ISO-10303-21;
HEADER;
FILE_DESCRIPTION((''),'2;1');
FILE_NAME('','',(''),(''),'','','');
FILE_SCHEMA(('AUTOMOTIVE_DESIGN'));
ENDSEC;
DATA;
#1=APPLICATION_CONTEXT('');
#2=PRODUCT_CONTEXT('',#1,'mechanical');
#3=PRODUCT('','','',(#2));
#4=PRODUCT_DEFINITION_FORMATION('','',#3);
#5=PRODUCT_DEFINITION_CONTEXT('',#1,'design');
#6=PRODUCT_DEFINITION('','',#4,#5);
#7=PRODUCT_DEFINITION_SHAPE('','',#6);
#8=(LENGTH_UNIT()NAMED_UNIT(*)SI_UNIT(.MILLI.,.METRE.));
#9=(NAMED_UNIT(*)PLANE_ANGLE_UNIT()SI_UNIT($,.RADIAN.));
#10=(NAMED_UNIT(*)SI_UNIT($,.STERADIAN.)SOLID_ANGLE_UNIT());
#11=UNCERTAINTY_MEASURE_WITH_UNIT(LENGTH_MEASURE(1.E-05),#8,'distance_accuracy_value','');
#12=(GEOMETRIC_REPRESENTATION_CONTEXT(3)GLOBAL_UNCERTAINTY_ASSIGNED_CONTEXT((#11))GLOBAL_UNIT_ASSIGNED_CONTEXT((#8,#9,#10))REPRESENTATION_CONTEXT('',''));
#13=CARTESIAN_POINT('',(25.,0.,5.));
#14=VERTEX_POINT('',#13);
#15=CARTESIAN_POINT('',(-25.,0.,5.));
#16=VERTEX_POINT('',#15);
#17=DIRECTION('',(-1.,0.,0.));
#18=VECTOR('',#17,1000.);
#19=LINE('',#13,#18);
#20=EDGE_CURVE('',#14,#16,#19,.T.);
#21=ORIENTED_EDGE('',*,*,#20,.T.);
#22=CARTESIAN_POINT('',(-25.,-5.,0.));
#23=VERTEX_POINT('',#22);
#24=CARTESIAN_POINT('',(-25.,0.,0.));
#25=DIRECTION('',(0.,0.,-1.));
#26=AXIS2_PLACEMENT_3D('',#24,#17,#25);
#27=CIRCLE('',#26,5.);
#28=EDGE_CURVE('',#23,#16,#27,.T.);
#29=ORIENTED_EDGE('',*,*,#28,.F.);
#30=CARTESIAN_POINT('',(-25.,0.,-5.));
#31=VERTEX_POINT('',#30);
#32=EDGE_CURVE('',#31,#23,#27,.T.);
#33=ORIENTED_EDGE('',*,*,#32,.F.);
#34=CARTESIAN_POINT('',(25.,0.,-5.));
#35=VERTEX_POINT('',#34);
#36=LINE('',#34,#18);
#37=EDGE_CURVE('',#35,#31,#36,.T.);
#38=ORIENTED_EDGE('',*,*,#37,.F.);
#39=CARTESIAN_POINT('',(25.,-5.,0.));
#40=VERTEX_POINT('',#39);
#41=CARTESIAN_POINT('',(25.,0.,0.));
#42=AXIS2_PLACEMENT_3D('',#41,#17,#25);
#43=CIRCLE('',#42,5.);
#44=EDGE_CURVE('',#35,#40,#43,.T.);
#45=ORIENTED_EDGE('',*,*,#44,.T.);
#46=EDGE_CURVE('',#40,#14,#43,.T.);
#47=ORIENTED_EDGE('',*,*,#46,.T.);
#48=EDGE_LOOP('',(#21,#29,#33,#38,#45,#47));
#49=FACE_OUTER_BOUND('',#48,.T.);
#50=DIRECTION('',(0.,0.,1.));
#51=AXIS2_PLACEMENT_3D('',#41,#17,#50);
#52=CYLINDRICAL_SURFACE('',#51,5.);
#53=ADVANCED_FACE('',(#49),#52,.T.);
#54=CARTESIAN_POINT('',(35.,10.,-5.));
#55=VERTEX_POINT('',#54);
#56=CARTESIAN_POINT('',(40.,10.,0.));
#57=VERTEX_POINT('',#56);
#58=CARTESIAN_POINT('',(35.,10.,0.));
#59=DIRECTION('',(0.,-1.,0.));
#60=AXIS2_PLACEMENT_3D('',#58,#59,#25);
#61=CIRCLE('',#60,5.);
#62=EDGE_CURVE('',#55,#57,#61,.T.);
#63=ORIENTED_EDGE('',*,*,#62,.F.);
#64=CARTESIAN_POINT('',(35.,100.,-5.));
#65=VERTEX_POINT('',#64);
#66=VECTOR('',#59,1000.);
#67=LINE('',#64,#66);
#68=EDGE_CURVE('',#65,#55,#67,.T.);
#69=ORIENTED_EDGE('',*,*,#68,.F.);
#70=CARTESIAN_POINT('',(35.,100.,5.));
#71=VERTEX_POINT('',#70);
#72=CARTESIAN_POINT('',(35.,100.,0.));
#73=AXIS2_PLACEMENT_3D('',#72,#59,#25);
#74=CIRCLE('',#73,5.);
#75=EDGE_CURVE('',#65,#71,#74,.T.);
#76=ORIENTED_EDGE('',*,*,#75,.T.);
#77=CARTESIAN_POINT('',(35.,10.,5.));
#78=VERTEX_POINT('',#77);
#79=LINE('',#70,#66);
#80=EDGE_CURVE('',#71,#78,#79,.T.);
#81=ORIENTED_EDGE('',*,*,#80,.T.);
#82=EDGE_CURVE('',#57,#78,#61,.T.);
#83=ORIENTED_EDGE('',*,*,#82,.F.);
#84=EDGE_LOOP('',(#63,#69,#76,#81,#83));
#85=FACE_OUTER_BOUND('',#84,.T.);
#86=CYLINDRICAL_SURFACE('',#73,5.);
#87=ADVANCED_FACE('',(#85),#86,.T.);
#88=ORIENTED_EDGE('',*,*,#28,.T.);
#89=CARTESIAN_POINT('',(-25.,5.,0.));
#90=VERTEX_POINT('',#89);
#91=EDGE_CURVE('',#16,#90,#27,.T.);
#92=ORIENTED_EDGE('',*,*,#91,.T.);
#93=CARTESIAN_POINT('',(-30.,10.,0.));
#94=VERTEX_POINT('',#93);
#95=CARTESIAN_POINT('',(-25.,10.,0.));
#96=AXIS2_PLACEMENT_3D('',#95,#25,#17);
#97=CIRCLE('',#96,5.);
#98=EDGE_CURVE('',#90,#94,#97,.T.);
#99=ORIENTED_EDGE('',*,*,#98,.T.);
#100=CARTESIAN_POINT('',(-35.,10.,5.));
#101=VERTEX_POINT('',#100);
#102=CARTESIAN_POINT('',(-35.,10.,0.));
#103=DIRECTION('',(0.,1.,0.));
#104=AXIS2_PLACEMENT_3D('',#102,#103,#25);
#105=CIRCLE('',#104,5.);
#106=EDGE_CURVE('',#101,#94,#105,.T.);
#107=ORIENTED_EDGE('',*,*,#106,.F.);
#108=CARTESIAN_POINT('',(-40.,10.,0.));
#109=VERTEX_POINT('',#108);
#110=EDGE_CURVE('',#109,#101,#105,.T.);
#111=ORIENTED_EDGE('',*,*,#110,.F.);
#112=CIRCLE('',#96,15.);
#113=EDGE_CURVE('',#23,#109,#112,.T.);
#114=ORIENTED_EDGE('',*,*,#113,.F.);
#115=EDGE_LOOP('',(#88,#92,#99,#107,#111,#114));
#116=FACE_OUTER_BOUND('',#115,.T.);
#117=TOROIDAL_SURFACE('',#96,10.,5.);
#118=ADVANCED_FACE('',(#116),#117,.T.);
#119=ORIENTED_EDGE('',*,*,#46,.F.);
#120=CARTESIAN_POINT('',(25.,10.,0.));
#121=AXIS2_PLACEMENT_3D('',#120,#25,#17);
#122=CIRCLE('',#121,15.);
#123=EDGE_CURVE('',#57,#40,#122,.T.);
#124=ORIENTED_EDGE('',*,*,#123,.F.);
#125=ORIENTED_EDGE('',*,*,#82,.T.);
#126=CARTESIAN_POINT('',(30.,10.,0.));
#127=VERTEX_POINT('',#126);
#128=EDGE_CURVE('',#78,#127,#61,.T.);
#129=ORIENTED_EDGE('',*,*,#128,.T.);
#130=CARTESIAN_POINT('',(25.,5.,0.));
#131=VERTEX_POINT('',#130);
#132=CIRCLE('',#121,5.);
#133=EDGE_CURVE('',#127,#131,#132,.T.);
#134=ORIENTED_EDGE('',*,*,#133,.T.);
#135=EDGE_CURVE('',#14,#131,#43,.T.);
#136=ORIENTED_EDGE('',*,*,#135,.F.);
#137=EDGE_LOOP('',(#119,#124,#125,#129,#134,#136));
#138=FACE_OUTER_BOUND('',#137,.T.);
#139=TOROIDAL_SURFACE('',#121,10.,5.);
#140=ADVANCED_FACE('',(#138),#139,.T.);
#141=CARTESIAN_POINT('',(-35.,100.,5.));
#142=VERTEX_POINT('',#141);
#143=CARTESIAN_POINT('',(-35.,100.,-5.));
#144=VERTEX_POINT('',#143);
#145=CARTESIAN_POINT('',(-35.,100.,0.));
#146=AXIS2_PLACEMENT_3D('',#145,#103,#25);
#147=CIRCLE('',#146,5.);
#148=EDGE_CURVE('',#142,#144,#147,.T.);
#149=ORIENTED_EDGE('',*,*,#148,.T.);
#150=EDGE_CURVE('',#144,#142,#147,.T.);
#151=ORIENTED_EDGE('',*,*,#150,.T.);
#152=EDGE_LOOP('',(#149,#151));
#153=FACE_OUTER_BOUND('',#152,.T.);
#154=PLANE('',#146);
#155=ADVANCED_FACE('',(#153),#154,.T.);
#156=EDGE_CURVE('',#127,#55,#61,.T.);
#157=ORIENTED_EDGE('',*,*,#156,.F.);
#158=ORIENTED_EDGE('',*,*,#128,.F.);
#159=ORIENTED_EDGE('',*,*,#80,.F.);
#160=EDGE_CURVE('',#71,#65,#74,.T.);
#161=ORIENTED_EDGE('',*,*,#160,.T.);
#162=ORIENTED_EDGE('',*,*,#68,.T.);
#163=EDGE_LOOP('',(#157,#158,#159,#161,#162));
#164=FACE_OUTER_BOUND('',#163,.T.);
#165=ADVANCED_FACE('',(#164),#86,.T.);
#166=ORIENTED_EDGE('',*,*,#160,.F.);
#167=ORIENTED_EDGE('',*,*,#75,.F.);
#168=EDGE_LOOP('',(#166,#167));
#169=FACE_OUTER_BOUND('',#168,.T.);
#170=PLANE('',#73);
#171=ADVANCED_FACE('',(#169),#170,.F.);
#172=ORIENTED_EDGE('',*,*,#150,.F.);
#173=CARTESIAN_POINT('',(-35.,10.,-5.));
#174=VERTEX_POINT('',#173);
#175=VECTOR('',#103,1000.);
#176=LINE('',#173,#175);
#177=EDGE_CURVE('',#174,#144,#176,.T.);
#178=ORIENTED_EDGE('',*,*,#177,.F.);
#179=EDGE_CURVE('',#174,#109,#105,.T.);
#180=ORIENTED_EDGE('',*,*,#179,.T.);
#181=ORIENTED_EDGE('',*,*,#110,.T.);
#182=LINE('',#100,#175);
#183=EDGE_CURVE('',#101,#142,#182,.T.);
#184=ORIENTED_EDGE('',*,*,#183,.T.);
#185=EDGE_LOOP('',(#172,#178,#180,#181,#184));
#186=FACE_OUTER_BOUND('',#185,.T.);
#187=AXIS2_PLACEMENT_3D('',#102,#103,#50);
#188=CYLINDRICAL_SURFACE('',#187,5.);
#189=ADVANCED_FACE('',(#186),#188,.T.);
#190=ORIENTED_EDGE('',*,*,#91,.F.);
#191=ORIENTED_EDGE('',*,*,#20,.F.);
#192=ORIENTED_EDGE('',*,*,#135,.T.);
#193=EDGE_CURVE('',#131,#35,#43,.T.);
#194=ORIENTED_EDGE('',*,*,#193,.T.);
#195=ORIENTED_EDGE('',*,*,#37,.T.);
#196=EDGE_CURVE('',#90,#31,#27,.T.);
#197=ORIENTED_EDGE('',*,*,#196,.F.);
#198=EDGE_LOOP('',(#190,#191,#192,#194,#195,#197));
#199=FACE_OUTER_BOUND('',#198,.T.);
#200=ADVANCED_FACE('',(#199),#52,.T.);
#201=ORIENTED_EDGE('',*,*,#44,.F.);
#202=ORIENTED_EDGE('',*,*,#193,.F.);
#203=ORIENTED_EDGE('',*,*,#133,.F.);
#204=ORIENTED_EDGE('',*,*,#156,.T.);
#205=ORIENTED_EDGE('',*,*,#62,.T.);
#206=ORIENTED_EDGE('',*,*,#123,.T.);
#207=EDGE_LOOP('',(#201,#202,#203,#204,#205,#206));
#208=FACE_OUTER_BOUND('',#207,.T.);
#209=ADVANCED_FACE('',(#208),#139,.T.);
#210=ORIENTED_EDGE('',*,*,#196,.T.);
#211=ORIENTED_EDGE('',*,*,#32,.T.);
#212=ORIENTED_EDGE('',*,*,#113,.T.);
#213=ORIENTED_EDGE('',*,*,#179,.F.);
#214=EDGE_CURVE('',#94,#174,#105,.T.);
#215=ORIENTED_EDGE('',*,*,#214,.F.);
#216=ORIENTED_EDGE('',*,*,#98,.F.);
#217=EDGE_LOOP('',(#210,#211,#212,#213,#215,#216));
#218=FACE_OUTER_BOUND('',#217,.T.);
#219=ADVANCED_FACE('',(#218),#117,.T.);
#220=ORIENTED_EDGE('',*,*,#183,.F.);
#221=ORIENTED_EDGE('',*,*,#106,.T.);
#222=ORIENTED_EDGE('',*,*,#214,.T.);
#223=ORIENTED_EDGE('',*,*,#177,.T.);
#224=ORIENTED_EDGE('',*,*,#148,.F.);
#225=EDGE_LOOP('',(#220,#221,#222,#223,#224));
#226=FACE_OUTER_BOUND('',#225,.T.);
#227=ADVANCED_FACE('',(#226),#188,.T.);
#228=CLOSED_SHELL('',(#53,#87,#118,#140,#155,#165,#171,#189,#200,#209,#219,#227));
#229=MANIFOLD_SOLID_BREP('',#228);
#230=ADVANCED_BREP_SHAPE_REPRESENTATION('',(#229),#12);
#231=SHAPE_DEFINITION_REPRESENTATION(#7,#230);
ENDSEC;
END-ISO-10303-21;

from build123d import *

# Parameters (mm, degrees)
SWEEP1_PROFILE_R = 5


with BuildPart() as part:
    # Sweep1: sweep along a path in Sketch1
    with BuildLine(Plane.XY) as sweep1_path:
        Line((-35, 100), (-35, 10))
        ThreePointArc((-35, 10), (-32.071067812, 2.928932188), (-25, 0))
        Line((-25, 0), (25, 0))
        ThreePointArc((25, 0), (32.071067812, 2.928932188), (35, 10))
        Line((35, 10), (35, 100))
    # Sweep1 profile (on start of the path) → Sweep1 (sweep)
    with BuildSketch(Plane(origin=(-35, 100, 0), x_dir=(0, 0, -1), z_dir=(0, -1, 0))):
        Circle(SWEEP1_PROFILE_R)
    sweep(path=sweep1_path.line)


solid = part.part
